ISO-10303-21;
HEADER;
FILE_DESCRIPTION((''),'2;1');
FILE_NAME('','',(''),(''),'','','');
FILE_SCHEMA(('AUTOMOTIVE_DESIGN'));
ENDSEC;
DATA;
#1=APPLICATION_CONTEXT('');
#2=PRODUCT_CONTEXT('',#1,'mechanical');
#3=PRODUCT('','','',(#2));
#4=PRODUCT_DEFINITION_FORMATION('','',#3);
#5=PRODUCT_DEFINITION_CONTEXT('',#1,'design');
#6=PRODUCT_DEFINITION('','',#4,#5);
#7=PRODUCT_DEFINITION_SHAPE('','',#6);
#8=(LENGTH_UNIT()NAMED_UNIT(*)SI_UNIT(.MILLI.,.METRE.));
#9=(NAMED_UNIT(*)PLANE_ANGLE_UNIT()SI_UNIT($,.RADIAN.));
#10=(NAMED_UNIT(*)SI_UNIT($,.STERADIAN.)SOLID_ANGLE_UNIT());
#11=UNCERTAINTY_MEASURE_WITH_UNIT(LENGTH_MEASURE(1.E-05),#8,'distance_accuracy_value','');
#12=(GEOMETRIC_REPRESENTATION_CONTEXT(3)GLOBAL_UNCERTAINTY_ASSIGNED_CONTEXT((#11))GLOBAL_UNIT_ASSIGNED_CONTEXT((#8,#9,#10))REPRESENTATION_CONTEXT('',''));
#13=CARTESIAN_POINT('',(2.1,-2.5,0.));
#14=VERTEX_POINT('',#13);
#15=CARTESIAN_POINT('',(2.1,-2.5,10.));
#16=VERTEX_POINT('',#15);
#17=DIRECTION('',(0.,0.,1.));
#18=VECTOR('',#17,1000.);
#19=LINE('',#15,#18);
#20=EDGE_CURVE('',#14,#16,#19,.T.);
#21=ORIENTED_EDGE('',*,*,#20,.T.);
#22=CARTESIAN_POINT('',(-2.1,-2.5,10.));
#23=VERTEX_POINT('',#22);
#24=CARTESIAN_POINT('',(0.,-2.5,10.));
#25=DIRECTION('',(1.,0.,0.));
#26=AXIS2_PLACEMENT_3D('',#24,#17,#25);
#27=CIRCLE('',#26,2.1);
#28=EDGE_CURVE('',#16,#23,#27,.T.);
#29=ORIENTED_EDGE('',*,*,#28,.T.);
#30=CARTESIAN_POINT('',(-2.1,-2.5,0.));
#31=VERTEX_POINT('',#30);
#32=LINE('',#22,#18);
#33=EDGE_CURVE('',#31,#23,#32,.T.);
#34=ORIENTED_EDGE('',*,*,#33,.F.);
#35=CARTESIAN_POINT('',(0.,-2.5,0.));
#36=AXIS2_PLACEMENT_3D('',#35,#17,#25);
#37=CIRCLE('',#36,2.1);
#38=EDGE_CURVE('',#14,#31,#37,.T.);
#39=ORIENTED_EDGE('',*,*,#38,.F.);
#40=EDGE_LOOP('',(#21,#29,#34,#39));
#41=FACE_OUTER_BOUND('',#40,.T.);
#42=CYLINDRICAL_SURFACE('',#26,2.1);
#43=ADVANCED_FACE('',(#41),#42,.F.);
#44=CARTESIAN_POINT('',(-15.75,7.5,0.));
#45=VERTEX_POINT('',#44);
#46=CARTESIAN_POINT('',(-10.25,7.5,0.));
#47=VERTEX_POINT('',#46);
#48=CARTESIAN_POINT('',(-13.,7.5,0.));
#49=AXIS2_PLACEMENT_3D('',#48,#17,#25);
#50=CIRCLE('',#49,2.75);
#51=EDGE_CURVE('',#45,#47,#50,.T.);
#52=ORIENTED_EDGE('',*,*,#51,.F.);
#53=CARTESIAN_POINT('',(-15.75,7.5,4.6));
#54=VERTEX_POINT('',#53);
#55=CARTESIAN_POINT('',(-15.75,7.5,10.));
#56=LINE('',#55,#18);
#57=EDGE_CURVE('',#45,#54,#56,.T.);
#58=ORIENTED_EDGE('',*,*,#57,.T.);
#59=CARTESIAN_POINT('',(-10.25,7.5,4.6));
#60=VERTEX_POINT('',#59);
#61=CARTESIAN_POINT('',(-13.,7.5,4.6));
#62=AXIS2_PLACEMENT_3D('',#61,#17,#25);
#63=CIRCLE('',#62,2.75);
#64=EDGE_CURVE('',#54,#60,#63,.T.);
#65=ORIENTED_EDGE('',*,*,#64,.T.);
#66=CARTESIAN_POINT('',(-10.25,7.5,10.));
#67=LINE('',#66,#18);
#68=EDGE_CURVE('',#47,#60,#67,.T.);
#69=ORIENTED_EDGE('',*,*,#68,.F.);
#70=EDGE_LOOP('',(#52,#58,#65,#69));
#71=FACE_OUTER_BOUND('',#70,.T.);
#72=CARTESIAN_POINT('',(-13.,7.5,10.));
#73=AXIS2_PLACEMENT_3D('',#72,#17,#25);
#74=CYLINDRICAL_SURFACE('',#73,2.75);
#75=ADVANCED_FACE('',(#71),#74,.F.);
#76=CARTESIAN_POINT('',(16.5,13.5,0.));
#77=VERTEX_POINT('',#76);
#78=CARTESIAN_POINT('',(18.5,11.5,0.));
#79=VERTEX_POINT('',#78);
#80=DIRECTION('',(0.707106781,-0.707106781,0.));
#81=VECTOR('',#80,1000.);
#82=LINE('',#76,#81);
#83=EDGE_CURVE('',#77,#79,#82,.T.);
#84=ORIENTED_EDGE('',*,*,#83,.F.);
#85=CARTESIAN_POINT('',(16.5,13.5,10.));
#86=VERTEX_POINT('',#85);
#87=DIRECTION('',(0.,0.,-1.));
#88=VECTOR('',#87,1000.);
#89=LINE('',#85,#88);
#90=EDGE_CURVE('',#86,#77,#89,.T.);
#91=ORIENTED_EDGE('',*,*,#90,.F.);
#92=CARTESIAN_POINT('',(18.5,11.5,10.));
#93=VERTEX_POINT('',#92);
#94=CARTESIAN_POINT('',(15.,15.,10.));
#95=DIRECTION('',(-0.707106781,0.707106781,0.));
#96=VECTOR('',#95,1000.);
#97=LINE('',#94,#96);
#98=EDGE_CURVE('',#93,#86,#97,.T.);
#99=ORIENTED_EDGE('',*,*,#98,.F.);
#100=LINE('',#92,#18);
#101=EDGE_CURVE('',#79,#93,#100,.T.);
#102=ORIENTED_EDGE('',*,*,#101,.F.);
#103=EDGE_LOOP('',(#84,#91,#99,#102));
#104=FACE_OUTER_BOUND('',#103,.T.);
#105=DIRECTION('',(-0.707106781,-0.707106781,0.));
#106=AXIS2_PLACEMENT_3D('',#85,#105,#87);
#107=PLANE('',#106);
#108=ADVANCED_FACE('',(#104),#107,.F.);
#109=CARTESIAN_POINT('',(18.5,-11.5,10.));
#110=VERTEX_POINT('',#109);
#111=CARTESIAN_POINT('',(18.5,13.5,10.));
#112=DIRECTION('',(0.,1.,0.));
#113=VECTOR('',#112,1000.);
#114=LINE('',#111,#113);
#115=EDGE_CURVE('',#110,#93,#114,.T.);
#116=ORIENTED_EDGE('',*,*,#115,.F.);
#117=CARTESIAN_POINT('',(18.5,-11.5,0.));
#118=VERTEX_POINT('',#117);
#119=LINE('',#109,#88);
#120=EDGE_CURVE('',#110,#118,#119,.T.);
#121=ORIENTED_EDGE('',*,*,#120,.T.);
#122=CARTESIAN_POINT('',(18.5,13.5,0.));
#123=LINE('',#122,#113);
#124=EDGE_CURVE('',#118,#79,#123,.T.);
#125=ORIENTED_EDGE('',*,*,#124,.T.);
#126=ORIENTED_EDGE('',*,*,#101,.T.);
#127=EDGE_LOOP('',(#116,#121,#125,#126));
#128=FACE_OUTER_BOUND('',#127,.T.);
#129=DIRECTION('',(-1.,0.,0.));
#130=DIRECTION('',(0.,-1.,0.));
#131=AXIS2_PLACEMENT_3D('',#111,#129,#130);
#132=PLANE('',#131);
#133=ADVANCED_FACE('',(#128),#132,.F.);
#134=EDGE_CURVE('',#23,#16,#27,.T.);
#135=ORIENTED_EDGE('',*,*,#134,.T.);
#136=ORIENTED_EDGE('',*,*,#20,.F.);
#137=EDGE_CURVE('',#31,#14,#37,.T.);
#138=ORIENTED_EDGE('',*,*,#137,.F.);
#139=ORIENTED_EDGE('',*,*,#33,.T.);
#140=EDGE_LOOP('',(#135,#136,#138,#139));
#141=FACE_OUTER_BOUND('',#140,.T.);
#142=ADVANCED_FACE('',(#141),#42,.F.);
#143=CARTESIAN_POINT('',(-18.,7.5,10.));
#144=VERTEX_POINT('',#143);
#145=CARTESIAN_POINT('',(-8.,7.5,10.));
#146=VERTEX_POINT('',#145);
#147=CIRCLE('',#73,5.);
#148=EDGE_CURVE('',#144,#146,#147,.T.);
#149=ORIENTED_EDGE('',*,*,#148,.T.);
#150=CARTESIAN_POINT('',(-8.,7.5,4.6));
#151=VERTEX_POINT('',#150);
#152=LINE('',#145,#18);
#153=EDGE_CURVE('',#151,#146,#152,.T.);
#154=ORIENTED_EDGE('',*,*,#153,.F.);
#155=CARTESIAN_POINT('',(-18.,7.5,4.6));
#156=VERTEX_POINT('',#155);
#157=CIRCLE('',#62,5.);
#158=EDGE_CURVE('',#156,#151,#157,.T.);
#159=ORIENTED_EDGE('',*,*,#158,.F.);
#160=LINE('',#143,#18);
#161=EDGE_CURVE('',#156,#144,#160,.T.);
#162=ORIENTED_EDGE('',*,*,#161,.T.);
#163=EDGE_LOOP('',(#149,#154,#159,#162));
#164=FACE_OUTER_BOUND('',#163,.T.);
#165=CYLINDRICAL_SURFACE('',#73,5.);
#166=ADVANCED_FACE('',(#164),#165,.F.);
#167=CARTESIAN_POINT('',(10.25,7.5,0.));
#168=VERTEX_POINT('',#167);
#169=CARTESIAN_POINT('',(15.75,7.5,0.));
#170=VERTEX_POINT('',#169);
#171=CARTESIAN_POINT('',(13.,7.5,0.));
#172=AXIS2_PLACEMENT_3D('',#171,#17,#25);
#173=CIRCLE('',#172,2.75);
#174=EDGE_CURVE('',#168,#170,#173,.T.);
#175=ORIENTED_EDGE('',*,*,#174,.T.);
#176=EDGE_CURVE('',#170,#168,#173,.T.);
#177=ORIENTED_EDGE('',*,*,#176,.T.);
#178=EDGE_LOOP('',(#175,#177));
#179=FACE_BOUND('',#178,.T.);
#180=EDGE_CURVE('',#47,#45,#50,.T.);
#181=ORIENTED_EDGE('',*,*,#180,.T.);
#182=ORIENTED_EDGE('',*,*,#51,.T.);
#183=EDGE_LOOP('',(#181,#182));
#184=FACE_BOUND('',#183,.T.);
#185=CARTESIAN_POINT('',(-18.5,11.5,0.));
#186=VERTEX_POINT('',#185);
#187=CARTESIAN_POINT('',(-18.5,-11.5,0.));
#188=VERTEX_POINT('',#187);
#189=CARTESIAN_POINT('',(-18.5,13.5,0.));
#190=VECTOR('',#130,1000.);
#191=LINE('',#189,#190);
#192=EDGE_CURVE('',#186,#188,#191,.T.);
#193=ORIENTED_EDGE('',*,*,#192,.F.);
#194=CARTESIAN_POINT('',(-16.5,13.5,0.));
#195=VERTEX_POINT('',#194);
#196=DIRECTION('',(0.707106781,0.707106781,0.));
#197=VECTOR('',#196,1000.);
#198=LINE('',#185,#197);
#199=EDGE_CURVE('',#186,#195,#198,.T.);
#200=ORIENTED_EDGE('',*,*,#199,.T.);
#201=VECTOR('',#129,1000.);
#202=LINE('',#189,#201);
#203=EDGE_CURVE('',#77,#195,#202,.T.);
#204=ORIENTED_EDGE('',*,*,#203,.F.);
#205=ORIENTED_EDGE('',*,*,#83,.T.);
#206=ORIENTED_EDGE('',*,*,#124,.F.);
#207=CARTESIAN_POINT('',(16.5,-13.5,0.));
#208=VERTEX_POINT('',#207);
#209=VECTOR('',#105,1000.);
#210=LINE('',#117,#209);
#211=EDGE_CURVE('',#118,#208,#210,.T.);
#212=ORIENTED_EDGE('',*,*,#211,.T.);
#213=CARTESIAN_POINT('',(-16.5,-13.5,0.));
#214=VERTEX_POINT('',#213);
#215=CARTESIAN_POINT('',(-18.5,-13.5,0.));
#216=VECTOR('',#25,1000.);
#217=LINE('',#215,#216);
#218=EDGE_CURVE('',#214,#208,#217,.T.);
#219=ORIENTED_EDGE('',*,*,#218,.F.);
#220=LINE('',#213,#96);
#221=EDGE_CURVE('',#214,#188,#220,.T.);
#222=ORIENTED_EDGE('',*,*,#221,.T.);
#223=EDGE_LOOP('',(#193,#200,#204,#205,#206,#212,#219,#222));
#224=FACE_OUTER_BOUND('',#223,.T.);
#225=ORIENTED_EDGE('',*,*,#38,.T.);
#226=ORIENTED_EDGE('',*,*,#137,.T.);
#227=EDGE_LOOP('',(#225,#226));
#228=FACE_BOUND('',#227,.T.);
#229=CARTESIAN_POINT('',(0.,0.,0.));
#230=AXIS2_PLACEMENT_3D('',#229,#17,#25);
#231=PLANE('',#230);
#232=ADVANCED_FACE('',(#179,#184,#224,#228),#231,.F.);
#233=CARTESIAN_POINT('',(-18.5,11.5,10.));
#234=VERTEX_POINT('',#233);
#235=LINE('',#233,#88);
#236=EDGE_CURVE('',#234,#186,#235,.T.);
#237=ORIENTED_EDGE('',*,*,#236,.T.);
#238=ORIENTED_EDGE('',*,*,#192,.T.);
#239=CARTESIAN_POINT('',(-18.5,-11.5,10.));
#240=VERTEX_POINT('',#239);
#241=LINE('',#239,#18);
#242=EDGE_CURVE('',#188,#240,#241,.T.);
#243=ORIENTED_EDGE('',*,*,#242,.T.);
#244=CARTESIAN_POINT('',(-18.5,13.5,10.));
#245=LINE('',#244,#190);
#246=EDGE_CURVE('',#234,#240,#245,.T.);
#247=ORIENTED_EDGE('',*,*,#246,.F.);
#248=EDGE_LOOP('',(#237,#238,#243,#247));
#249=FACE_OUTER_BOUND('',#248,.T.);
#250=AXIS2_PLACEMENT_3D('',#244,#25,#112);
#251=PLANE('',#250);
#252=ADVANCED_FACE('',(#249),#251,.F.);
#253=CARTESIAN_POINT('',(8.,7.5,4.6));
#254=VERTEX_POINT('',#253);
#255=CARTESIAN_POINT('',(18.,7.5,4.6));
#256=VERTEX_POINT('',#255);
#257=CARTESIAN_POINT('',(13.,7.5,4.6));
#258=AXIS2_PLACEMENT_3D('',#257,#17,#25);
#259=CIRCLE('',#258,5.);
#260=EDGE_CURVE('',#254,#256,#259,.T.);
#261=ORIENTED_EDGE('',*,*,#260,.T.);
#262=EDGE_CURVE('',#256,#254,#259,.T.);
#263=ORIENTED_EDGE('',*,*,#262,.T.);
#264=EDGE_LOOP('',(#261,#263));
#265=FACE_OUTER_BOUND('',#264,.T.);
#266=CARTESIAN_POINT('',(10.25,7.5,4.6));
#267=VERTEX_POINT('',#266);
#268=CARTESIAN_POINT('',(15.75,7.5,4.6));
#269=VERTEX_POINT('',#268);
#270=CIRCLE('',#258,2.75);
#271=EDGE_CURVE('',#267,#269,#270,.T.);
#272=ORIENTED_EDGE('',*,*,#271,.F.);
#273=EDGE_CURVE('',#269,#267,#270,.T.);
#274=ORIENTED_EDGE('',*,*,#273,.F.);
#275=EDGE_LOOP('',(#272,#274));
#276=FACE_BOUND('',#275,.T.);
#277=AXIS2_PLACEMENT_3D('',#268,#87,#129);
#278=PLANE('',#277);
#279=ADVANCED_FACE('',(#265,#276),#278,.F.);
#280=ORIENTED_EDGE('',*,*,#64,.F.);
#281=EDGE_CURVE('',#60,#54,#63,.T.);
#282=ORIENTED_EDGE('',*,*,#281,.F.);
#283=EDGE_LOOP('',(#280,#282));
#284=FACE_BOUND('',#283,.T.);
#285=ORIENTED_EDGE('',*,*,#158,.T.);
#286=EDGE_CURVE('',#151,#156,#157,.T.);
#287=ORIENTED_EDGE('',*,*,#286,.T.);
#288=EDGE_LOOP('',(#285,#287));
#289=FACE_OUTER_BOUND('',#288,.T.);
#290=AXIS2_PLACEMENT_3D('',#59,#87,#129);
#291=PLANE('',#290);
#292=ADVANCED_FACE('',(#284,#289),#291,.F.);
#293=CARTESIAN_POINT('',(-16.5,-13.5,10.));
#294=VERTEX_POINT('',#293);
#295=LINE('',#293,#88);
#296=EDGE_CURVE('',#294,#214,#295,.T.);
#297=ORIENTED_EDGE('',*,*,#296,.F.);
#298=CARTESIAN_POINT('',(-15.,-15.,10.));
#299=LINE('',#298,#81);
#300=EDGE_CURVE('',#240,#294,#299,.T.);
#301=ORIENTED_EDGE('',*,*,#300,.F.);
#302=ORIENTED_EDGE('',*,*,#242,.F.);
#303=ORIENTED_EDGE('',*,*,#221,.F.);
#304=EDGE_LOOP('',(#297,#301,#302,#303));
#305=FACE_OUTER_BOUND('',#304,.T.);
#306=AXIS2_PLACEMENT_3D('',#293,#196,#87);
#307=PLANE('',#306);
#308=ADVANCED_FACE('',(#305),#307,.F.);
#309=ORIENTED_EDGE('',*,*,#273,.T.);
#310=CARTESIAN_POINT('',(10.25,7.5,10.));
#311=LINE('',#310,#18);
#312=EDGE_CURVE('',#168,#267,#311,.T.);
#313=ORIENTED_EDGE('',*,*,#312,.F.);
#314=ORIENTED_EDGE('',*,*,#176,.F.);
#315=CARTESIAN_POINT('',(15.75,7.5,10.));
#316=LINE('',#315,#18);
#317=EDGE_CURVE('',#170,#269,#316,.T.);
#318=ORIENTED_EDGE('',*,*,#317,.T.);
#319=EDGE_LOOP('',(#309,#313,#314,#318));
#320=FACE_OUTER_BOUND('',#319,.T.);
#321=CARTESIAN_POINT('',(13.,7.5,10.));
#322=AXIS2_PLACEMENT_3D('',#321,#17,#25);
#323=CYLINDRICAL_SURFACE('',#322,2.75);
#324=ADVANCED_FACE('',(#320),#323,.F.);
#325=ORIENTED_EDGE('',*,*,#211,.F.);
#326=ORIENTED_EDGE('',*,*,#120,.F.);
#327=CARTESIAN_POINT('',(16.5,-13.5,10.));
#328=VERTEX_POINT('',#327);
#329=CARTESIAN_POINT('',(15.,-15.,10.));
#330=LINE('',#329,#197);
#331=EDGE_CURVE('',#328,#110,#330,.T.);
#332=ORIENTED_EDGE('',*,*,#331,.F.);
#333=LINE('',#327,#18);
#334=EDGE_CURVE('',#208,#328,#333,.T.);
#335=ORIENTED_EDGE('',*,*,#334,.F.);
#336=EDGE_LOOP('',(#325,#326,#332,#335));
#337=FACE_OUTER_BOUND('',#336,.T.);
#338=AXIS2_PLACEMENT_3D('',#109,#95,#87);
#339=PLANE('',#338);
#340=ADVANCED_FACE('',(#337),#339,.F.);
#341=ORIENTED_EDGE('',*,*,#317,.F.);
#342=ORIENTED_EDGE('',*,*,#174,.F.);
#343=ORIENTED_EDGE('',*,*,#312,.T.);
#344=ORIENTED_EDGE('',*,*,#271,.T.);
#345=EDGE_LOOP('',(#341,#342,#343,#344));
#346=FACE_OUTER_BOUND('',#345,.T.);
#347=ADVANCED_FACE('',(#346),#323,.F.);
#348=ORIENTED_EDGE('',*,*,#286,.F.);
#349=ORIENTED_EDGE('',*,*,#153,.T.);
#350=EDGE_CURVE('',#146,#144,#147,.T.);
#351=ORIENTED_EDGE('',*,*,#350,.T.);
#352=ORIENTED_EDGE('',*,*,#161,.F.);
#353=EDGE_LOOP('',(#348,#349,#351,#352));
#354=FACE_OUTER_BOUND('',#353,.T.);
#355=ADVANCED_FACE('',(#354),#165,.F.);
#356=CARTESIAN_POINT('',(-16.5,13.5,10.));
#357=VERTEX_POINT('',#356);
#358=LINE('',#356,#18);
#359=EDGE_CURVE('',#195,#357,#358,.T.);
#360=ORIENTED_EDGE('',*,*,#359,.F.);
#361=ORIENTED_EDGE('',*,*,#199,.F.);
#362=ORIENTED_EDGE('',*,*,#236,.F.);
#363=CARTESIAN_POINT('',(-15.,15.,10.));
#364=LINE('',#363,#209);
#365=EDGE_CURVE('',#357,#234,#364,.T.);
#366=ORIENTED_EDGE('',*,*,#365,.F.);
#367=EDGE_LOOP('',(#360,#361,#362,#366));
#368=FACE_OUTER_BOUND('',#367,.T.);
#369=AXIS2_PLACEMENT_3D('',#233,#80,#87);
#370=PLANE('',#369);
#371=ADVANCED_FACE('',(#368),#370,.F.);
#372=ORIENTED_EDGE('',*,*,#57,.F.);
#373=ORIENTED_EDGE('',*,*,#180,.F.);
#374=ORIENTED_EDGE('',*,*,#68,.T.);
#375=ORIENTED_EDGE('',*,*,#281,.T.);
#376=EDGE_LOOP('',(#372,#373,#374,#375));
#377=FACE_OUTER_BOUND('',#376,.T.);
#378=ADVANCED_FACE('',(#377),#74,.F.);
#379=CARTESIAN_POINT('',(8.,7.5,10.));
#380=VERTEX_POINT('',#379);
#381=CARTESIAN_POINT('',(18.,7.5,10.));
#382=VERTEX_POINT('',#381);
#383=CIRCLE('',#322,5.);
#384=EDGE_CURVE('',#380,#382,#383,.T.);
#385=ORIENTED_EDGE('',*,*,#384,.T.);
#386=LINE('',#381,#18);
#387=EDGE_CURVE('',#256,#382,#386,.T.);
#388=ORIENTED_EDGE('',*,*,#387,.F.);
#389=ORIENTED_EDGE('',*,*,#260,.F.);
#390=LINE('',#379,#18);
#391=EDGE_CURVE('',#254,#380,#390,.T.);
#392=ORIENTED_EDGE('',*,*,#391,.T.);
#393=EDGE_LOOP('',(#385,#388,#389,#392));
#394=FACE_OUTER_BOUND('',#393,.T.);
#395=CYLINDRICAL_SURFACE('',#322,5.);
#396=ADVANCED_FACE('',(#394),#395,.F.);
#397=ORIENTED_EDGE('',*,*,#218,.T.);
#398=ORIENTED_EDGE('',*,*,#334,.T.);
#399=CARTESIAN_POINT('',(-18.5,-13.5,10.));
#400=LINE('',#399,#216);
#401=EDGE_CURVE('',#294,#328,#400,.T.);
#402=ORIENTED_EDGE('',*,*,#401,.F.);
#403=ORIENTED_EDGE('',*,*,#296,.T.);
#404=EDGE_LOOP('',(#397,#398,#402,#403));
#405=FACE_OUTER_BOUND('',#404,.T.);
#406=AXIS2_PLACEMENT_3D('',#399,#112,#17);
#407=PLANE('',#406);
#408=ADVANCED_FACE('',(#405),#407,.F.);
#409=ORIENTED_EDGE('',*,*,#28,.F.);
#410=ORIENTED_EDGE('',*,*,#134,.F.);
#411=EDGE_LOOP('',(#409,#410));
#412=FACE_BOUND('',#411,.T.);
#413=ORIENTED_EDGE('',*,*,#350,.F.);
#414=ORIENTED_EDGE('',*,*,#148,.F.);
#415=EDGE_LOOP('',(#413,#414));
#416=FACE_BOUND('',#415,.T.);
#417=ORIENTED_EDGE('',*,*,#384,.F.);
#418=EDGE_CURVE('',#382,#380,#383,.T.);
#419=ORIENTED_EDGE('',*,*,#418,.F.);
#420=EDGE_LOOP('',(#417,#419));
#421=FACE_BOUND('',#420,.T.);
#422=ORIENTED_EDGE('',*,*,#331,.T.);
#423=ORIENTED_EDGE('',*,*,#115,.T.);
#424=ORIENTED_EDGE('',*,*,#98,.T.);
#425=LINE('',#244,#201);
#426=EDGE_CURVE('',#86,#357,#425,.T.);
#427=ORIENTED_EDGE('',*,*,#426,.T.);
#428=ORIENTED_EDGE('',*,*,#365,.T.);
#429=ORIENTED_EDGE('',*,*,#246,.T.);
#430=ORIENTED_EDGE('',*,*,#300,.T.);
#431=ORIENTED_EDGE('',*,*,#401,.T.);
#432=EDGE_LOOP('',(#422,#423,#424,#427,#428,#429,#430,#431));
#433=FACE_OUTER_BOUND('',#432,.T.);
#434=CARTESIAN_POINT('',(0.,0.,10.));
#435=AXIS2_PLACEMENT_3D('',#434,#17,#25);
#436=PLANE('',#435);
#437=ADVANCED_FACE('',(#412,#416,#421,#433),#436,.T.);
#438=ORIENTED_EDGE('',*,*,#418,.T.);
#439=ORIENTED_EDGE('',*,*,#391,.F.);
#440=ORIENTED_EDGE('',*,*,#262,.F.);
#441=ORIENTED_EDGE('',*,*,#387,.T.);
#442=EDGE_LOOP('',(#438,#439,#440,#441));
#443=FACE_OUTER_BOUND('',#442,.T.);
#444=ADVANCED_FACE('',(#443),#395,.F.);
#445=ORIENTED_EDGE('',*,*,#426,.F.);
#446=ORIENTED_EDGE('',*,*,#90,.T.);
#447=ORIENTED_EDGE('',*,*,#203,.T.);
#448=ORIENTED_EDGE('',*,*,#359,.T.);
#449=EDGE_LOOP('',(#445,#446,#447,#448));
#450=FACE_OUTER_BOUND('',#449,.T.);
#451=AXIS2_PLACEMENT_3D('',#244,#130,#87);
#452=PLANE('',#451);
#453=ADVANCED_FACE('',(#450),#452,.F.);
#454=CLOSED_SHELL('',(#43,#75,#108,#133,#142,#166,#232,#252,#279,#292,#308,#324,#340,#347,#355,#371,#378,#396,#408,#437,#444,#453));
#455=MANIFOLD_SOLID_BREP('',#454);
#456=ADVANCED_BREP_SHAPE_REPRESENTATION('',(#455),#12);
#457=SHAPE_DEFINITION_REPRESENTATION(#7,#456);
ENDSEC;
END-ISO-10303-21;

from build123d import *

# Parameters (mm, degrees)
SKETCH1_W                                           = 37
SKETCH1_H                                           = 27
BOSS_EXTRUDE1_DEPTH                                 = 10
CBORE_FOR_M5_HEX_SOCKET_HEAD_CAP_SCREW1_D           = 5.5
CBORE_FOR_M5_HEX_SOCKET_HEAD_CAP_SCREW1_CBORE_D     = 10
CBORE_FOR_M5_HEX_SOCKET_HEAD_CAP_SCREW1_CBORE_DEPTH = 5.4
M5_TAPPED_HOLE1_D                                   = 4.2
M5_TAPPED_HOLE1_DEPTH                               = 12.4
M5_TAPPED_HOLE1_TIP                                 = 1.2618073
CHAMFER1_SIZE                                       = 2


with BuildPart() as part:
    # Sketch1 → Boss-Extrude1 (new body)
    with BuildSketch(Plane.XY):
        Rectangle(SKETCH1_W, SKETCH1_H)
    extrude(amount=BOSS_EXTRUDE1_DEPTH)

    # CBORE for M5 Hex Socket Head Cap Screw1 (through all)
    with Locations(Plane.XY.offset(10)):
        with Locations((-13, 7.5), (13, 7.5)):
            CounterBoreHole(CBORE_FOR_M5_HEX_SOCKET_HEAD_CAP_SCREW1_D / 2, CBORE_FOR_M5_HEX_SOCKET_HEAD_CAP_SCREW1_CBORE_D / 2, CBORE_FOR_M5_HEX_SOCKET_HEAD_CAP_SCREW1_CBORE_DEPTH)

    # M5 Tapped Hole1
    with Locations(Plane.XY.offset(10)):
        with Locations((0, -2.5)):
            Hole(M5_TAPPED_HOLE1_D / 2, depth=M5_TAPPED_HOLE1_DEPTH)
            with Locations((0, 0, -(M5_TAPPED_HOLE1_DEPTH + M5_TAPPED_HOLE1_TIP / 2))):  # 118° drill point
                Cone(0, M5_TAPPED_HOLE1_D / 2, M5_TAPPED_HOLE1_TIP, mode=Mode.SUBTRACT)

    # Chamfer1
    chamfer1_edges = [part.edges().sort_by_distance(p)[0] for p in [
        (18.5, -13.5, 5),
        (-18.5, -13.5, 5),
        (-18.5, 13.5, 5),
        (18.5, 13.5, 5),
    ]]
    chamfer(chamfer1_edges, length=CHAMFER1_SIZE)


solid = part.part
